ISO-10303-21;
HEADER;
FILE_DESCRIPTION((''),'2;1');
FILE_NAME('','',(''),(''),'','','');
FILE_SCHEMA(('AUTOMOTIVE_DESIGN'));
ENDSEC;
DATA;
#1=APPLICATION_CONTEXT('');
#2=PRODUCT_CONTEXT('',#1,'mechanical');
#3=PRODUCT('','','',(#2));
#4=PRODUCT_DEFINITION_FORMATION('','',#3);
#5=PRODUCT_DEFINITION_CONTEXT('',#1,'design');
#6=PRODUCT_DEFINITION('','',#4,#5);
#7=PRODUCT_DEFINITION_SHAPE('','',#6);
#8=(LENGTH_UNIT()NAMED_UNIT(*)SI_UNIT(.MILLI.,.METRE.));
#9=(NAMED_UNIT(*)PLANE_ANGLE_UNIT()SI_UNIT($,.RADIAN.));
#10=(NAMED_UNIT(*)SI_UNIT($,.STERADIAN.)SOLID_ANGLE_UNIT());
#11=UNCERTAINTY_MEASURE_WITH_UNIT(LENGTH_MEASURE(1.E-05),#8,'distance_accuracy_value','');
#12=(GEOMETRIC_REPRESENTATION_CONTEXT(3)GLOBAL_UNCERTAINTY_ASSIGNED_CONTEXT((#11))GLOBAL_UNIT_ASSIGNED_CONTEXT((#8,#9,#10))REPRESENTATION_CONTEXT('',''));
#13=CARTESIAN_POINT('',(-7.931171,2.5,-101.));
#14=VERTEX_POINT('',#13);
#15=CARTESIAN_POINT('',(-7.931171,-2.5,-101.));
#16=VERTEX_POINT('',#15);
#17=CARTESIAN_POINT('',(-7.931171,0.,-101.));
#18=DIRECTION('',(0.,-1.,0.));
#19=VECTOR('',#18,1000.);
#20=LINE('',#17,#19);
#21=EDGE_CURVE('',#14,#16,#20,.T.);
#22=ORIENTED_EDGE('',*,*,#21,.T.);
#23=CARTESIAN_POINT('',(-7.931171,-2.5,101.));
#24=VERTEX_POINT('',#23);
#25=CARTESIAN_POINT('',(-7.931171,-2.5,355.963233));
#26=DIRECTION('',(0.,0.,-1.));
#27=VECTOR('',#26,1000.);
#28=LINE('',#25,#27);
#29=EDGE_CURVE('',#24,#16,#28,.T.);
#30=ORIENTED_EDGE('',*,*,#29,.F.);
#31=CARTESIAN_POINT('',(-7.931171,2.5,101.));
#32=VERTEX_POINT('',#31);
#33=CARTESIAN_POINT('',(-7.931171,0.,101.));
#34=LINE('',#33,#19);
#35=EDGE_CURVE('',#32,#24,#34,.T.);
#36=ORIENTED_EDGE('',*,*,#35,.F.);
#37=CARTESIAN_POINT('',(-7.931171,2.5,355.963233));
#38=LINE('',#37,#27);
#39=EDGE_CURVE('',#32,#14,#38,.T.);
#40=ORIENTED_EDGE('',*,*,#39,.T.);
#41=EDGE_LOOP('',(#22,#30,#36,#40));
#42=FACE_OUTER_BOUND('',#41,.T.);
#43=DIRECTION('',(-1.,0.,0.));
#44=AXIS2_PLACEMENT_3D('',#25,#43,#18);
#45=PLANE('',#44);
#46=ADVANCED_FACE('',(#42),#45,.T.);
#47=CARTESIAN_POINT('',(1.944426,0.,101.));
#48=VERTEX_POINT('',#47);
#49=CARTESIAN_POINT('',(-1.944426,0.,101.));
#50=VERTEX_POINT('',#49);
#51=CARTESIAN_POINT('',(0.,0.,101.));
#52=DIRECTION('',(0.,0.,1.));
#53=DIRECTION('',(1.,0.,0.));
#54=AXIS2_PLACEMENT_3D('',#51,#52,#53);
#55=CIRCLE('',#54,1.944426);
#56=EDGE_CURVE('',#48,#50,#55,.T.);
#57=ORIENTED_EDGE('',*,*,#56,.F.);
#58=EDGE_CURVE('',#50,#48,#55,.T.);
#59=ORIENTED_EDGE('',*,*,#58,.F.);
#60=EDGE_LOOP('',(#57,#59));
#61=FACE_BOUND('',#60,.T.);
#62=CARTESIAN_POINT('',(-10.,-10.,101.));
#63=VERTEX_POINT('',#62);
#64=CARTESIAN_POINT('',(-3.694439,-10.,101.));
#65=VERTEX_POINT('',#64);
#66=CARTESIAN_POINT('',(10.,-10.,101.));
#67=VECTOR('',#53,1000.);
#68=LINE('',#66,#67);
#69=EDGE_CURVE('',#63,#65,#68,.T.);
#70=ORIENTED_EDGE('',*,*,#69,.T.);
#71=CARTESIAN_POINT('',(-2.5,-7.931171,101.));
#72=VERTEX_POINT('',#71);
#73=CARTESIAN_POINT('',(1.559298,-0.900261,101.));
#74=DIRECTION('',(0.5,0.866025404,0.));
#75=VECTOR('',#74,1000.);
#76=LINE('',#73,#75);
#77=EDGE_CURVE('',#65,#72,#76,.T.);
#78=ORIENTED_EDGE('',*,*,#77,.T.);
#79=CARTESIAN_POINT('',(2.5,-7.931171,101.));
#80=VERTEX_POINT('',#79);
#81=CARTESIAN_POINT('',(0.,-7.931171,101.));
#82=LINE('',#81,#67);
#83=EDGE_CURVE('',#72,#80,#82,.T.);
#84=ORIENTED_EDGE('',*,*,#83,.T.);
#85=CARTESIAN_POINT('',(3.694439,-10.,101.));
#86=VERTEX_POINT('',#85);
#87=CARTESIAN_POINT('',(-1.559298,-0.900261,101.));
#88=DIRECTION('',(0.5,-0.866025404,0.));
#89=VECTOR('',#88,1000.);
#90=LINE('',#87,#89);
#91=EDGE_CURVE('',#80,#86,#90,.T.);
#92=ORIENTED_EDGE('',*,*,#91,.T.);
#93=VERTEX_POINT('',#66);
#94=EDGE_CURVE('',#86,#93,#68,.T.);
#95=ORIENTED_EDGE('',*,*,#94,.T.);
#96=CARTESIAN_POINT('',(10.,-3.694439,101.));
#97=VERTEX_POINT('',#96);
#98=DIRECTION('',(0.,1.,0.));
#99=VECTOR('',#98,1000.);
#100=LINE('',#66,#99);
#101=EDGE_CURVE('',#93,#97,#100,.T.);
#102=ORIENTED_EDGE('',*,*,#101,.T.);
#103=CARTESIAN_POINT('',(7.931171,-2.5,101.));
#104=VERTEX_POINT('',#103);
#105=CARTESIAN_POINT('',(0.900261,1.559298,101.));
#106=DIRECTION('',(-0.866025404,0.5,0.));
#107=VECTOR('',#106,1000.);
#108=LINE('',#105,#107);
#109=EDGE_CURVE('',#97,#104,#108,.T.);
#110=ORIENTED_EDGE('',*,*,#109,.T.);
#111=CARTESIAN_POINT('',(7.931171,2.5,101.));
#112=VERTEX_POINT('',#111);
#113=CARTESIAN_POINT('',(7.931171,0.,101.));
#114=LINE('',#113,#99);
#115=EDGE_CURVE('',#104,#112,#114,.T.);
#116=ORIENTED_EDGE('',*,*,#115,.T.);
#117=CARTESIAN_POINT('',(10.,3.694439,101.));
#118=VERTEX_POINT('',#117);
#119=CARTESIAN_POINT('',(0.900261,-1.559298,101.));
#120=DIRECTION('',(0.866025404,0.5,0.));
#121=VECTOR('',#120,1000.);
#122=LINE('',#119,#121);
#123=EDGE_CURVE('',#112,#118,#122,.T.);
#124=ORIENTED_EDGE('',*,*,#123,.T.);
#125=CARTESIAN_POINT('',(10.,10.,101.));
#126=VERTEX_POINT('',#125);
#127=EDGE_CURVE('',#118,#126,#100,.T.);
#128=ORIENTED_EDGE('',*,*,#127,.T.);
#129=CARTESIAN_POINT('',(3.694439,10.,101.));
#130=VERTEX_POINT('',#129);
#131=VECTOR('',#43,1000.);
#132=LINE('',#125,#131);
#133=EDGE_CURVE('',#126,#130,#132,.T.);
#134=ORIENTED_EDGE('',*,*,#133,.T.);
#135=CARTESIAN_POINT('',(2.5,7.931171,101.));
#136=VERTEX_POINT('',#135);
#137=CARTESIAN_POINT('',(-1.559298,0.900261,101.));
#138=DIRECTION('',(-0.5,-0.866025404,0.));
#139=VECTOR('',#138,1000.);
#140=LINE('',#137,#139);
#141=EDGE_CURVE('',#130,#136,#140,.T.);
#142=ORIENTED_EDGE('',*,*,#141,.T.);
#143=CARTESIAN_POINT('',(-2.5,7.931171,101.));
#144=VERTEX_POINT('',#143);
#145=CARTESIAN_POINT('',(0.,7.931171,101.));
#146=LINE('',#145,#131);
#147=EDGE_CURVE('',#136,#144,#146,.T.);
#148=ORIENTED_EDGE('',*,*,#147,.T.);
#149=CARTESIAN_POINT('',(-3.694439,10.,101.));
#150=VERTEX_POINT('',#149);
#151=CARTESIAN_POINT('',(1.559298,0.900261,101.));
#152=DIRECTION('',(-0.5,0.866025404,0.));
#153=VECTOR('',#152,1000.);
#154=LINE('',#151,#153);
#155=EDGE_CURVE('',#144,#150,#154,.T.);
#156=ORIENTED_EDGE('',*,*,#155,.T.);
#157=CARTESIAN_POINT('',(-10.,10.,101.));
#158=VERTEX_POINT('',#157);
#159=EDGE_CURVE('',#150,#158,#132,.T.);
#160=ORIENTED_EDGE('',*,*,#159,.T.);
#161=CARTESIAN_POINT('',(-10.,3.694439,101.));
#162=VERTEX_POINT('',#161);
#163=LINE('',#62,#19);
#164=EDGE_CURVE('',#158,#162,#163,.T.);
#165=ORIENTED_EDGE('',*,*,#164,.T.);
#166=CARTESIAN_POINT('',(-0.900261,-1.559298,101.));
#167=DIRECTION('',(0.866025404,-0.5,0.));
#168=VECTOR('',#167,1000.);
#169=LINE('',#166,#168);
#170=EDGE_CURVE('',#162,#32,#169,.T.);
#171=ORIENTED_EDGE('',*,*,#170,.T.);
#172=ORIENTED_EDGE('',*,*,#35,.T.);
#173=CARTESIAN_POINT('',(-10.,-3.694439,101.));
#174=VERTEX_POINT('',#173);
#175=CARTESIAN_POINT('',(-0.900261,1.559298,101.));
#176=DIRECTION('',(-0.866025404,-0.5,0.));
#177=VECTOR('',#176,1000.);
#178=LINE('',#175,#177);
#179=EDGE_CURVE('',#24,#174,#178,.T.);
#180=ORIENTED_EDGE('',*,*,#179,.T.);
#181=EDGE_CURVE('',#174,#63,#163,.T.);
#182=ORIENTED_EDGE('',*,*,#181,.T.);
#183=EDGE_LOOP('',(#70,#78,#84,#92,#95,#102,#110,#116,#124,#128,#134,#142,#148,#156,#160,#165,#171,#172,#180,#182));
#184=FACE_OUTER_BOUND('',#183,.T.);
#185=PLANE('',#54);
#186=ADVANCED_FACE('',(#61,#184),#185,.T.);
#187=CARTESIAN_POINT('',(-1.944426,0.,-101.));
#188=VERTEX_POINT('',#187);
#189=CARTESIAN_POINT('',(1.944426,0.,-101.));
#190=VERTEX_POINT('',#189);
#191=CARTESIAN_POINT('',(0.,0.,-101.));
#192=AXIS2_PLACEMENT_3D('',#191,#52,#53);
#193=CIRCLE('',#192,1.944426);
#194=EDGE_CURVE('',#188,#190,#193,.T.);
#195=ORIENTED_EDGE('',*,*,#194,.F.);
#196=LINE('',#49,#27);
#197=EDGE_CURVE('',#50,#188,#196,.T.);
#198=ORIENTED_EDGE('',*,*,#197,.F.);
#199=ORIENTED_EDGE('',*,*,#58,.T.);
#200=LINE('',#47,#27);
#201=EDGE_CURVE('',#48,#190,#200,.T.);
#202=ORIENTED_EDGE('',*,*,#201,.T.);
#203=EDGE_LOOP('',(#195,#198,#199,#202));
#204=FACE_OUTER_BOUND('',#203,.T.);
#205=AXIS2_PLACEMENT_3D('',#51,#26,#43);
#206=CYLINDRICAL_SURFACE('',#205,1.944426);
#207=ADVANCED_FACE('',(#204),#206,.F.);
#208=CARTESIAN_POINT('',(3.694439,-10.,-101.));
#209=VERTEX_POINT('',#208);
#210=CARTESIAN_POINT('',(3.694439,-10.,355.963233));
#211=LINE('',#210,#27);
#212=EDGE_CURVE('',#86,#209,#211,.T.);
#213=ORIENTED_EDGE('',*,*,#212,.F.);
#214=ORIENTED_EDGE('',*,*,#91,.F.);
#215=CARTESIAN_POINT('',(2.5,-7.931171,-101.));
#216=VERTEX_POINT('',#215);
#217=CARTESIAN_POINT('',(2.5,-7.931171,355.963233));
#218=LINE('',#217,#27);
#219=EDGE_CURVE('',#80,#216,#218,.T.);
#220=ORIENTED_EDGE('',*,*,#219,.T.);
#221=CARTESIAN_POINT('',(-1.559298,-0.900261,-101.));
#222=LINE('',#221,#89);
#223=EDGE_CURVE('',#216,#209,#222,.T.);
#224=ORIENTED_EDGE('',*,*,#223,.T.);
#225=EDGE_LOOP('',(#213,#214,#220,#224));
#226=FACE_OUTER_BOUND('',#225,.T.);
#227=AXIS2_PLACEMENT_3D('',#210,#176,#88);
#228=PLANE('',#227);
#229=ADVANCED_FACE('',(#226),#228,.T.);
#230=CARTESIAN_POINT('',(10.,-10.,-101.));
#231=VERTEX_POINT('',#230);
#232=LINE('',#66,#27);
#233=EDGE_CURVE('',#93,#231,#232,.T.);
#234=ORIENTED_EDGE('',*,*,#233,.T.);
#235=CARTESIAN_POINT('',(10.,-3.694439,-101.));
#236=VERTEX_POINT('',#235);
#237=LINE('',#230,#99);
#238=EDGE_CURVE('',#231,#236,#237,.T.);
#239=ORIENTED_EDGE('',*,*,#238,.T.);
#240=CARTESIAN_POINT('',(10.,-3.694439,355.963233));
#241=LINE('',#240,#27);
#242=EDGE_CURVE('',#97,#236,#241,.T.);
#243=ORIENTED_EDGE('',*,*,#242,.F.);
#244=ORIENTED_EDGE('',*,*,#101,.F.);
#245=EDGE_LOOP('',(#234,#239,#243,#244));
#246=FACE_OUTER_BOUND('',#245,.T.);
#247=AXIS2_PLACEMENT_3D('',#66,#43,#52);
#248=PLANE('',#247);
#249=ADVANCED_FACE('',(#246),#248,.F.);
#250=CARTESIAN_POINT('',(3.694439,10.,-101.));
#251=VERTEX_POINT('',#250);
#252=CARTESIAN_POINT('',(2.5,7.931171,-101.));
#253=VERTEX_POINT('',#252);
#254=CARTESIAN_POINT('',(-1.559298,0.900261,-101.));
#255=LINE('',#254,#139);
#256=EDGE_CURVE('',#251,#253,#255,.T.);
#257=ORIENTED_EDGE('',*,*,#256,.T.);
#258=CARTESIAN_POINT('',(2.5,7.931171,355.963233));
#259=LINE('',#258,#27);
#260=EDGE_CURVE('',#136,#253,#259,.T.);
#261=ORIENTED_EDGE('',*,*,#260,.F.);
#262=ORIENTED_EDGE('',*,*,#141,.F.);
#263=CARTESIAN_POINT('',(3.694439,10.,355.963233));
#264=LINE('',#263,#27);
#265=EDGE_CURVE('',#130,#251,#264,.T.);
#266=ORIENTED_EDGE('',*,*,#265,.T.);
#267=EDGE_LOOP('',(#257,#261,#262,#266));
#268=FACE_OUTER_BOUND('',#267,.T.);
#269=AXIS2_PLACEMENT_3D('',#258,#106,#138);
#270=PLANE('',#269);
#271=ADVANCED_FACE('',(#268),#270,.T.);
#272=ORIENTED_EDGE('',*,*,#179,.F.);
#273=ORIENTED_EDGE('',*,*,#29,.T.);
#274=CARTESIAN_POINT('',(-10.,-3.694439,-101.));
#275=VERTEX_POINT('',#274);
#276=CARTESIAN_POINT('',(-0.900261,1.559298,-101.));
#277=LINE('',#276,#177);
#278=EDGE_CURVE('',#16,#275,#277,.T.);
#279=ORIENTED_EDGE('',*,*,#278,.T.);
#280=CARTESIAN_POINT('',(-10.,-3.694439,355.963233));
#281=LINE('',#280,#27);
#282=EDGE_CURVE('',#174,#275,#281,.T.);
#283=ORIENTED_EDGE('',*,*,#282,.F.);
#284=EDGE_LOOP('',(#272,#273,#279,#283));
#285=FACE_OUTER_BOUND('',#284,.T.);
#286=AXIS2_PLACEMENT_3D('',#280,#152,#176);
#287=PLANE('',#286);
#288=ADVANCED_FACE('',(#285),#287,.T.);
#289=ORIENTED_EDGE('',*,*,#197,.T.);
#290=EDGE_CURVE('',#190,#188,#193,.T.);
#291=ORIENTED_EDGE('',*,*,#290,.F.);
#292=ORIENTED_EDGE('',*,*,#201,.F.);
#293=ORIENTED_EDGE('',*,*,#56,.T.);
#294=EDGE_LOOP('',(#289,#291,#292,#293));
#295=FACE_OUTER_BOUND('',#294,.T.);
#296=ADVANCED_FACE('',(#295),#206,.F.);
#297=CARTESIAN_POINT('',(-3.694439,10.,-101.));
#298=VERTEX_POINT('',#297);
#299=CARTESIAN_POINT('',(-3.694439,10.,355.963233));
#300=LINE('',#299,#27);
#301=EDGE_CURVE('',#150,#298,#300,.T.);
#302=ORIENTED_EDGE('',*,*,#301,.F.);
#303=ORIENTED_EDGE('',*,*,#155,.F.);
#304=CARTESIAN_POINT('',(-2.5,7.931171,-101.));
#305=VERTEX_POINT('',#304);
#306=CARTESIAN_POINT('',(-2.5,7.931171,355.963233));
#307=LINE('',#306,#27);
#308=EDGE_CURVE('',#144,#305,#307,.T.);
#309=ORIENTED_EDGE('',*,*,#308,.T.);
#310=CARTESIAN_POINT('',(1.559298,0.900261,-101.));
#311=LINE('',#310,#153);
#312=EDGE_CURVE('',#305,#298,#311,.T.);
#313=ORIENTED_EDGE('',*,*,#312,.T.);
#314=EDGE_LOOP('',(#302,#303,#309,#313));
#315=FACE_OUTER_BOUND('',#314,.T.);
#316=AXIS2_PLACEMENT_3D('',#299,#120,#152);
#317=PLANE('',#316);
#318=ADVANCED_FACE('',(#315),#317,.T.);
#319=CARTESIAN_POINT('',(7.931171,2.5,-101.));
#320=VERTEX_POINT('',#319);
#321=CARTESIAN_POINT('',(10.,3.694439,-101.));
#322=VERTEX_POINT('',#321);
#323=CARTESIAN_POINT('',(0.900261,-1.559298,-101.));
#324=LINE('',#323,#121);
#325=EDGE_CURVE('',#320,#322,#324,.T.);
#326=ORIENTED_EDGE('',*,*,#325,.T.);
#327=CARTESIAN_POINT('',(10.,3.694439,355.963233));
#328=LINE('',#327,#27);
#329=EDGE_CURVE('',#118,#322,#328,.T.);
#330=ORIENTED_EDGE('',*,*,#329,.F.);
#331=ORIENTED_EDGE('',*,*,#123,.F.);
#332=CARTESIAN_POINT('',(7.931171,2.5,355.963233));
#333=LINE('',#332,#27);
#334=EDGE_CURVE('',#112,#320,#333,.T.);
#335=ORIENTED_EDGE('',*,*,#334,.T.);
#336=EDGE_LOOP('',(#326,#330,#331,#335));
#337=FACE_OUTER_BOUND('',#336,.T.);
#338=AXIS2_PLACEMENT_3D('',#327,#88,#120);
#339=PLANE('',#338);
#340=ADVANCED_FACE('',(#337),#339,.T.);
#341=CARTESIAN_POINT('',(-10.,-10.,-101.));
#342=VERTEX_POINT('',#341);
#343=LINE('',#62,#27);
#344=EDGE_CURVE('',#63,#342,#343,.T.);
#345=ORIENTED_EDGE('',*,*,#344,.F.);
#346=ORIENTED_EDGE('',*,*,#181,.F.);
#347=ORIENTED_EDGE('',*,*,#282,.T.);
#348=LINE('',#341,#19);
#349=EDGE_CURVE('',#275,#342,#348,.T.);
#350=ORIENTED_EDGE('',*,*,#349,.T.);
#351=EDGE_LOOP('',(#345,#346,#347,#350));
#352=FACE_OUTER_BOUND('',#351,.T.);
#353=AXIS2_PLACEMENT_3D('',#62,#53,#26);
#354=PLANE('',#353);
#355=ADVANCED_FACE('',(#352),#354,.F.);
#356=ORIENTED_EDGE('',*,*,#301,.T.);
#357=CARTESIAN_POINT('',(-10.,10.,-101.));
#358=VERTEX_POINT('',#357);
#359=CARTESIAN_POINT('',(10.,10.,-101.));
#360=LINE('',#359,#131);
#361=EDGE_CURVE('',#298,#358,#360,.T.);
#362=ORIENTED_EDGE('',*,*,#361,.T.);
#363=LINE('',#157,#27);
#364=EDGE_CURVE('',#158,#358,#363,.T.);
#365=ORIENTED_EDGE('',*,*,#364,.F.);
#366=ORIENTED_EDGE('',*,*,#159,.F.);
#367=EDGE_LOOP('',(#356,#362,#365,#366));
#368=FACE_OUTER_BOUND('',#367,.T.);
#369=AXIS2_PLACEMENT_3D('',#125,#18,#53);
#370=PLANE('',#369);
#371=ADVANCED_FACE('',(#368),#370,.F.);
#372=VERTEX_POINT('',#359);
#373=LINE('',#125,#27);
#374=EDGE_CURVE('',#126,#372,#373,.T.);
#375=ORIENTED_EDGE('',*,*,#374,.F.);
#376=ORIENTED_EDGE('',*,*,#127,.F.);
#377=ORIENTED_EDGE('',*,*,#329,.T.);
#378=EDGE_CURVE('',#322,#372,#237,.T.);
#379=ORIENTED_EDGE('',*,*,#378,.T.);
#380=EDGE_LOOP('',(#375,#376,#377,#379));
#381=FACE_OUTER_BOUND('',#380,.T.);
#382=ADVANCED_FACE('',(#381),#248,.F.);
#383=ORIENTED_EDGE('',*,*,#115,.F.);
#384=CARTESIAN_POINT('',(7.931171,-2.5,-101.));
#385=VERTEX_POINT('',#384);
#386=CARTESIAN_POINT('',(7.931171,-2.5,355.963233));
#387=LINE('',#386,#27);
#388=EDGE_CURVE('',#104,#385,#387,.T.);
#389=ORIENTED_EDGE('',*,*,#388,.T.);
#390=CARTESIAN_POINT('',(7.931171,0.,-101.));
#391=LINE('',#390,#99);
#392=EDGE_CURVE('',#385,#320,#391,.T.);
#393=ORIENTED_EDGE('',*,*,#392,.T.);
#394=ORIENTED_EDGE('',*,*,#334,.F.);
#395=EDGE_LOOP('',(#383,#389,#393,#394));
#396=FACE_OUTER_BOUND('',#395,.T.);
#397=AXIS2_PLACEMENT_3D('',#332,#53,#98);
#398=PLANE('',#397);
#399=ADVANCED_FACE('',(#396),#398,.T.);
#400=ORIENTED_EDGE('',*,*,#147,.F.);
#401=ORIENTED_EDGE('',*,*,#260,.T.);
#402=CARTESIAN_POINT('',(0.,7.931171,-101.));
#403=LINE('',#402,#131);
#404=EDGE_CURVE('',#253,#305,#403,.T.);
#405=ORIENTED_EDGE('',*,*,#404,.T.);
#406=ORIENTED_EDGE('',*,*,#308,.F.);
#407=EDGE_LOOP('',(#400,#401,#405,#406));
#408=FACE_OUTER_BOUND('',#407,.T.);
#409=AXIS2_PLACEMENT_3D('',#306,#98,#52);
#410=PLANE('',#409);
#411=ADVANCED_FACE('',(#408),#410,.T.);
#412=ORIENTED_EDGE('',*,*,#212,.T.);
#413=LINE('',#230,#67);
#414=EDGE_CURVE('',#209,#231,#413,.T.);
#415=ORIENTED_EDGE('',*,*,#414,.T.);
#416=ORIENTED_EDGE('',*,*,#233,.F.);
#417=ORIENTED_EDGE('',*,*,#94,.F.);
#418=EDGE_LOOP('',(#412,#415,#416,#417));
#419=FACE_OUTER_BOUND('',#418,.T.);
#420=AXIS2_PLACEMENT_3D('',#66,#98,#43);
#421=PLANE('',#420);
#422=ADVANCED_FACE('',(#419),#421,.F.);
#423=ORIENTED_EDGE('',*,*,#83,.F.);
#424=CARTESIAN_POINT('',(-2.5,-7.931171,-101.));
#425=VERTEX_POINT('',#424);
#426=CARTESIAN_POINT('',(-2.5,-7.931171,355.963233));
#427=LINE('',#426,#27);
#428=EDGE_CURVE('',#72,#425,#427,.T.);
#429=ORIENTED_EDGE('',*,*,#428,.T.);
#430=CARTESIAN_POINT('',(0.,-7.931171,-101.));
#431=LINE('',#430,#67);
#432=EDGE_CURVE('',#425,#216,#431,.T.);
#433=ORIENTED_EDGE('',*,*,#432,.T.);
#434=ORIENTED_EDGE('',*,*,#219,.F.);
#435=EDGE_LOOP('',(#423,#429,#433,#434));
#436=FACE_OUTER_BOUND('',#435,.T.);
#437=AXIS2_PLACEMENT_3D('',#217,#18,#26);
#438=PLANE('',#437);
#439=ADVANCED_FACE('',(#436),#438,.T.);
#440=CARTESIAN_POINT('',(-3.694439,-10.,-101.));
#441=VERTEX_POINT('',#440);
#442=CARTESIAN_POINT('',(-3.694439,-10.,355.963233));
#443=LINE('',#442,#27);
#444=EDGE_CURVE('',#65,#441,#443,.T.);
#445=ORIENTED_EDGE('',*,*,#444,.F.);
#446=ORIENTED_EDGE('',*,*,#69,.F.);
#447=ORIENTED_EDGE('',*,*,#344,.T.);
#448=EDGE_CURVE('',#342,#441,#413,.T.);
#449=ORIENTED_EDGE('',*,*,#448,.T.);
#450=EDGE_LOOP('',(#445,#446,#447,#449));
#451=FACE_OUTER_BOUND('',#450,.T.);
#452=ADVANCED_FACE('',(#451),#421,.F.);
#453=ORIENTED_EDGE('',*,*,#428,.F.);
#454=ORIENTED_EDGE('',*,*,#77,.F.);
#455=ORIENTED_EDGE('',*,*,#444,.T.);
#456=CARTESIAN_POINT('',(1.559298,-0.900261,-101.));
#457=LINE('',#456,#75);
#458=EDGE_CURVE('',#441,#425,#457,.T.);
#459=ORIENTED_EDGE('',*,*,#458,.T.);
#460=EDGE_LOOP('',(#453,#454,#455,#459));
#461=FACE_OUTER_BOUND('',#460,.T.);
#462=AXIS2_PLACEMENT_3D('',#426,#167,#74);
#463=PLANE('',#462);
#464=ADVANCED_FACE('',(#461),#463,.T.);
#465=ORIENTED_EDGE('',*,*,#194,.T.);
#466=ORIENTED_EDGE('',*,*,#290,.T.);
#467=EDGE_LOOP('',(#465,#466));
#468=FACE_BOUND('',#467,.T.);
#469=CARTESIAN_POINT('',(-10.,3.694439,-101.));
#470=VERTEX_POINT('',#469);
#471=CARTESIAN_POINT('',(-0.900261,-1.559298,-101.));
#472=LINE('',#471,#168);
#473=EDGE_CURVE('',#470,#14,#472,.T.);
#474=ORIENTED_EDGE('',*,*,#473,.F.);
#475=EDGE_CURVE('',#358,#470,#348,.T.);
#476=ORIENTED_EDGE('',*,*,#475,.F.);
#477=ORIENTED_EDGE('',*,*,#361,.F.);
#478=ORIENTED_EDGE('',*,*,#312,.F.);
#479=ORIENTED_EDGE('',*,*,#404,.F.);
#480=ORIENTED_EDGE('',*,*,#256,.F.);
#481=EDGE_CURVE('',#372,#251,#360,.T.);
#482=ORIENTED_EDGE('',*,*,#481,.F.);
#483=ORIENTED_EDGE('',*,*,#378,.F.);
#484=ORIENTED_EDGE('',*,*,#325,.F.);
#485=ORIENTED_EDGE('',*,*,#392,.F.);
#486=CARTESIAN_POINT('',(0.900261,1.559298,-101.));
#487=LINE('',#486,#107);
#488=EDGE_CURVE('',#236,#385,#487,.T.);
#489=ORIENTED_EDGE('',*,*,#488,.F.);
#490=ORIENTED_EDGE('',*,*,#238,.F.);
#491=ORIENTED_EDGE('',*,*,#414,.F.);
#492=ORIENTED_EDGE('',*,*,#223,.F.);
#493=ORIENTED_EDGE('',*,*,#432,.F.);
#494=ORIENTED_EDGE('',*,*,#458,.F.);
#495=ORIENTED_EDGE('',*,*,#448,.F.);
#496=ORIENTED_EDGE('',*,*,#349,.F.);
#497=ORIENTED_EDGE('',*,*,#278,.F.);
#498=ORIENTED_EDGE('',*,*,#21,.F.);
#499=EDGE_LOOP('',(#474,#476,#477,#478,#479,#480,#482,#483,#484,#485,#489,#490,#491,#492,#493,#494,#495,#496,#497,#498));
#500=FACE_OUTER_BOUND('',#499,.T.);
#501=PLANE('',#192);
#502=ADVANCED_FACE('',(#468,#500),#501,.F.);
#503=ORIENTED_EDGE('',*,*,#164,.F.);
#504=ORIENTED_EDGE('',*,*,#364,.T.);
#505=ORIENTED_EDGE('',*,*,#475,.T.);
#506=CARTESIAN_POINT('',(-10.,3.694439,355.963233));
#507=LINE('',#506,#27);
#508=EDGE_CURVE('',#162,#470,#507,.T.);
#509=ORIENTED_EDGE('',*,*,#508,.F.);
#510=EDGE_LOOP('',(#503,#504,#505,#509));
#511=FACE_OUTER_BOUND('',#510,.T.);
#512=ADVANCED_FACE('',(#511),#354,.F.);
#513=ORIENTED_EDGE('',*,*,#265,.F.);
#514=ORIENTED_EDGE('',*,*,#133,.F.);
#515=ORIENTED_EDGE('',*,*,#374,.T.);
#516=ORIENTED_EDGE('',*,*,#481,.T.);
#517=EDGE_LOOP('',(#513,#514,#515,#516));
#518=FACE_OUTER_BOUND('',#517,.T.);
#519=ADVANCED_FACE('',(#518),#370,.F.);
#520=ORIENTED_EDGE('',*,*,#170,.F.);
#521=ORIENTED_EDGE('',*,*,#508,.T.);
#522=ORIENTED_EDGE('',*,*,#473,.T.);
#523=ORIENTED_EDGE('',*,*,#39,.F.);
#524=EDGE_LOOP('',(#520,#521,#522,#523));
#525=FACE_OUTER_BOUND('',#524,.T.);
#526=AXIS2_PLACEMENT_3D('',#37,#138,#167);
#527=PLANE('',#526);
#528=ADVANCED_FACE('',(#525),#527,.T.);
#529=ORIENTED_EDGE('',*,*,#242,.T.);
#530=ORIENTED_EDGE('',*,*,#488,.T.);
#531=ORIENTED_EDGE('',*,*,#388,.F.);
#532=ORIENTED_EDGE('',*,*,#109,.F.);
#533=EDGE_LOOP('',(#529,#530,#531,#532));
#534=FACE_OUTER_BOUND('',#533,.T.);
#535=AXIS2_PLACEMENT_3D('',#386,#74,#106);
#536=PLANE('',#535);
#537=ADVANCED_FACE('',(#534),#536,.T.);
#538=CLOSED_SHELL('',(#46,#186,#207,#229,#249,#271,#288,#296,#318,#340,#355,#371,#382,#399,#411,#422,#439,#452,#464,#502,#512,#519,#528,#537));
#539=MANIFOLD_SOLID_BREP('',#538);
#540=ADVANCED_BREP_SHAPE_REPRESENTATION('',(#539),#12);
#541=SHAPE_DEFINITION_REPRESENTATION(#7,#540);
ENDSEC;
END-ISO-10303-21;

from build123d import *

# Parameters (mm, degrees)
SKETCH_1_W               = 20
SKETCH_1_H               = 20
SKETCH_1_R               = 1.94442565
EXTRUDE_1_DEPTH          = 101
CUT_EXTRUDE_1_DEPTH      = 203.494444368
PATTERN_CIRCULAR_1_COUNT = 4


with BuildPart() as part:
    # 草图1 → 凸台-拉伸1 (new, symmetric)
    with BuildSketch(Plane.XY):
        Rectangle(SKETCH_1_W, SKETCH_1_H)
        Circle(SKETCH_1_R, mode=Mode.SUBTRACT)
    extrude(amount=EXTRUDE_1_DEPTH, both=True)

    # 草图2 → 切除-拉伸1 (cut, symmetric)
    with BuildSketch(Plane.XY.offset(101)):
        Polygon((-32.933615203, 60.643738676), (-3.694439046, 10), (-2.5, 7.931170886), (2.5, 7.931170886), (3.694439046, 10), (32.933615203, 60.643738676), (32.933615203, 177.600443305), (-32.933615203, 177.600443305), align=None)
    cut_extrude_1 = extrude(amount=CUT_EXTRUDE_1_DEPTH, both=True, mode=Mode.SUBTRACT)

    # 阵列(圆周)1: 切除-拉伸1 ×4 about axis
    pattern_circular_1_axis = Axis((0, 0, 101), (0, 0, -1))
    for i in range(1, PATTERN_CIRCULAR_1_COUNT):
        add(cut_extrude_1.rotate(pattern_circular_1_axis, i * 360 / PATTERN_CIRCULAR_1_COUNT), mode=Mode.SUBTRACT)


solid = part.part
